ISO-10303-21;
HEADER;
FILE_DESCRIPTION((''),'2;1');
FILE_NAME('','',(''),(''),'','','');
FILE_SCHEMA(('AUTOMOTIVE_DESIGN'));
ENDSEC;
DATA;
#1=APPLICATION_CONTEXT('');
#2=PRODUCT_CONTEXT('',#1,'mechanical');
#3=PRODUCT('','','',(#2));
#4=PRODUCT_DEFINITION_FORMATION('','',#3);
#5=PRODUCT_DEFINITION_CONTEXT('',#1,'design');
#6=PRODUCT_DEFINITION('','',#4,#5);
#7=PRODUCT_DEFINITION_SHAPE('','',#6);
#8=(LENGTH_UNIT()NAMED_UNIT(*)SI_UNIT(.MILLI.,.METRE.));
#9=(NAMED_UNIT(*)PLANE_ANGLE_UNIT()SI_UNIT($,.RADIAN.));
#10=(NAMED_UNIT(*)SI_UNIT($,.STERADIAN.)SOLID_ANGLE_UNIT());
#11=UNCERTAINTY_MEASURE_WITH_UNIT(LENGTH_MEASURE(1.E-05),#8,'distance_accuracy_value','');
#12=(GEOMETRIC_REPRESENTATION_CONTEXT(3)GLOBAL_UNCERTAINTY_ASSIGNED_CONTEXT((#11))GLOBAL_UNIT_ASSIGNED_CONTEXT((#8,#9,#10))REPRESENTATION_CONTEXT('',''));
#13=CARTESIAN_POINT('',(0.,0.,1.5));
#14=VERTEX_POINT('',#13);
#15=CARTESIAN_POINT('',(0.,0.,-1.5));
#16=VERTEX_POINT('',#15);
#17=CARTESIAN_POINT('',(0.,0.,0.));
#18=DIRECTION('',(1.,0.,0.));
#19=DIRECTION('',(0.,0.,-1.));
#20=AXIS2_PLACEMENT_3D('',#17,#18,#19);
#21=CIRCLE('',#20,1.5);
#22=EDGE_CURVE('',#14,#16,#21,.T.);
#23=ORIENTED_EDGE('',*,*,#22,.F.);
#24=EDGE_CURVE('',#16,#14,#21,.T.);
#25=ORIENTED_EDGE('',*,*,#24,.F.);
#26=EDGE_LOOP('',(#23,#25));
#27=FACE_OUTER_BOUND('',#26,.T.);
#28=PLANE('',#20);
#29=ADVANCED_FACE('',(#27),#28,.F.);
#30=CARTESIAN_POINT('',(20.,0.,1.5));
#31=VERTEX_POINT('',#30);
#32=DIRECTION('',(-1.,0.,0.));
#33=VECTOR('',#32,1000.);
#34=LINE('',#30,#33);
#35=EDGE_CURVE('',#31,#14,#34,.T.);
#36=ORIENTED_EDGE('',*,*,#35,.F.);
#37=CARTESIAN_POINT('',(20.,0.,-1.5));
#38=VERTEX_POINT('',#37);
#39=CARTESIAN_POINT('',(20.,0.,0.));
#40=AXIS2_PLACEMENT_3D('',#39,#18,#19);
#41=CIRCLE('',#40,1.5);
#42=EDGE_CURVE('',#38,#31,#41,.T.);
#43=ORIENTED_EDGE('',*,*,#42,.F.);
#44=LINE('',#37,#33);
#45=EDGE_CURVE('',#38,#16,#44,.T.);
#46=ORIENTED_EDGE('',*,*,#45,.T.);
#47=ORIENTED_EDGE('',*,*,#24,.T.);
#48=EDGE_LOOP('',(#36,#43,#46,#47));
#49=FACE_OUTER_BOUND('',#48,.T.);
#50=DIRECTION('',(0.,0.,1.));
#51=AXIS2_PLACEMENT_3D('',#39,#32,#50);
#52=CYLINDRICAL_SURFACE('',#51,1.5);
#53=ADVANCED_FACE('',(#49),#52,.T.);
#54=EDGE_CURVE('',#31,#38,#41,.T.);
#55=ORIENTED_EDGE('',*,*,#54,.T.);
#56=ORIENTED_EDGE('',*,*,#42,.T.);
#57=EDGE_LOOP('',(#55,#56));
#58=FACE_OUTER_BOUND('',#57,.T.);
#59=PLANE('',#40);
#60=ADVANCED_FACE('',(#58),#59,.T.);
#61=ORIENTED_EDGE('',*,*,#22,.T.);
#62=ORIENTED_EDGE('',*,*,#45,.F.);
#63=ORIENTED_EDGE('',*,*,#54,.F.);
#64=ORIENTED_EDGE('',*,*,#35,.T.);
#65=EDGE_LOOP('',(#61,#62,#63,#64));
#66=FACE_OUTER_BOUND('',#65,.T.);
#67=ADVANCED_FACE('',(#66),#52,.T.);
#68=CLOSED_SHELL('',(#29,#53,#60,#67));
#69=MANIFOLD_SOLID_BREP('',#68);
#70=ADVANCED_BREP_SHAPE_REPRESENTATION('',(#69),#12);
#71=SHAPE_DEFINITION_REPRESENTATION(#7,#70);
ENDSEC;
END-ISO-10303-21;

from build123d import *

# Parameters (mm, degrees)
SKETCH1_R           = 1.5
BOSS_EXTRUDE1_DEPTH = 20


with BuildPart() as part:
    # Sketch1 → Boss-Extrude1 (new body)
    with BuildSketch(Plane(origin=(0, 0, 0), x_dir=(0, 0, -1), z_dir=(1, 0, 0))):
        Circle(SKETCH1_R)
    extrude(amount=BOSS_EXTRUDE1_DEPTH)


solid = part.part
